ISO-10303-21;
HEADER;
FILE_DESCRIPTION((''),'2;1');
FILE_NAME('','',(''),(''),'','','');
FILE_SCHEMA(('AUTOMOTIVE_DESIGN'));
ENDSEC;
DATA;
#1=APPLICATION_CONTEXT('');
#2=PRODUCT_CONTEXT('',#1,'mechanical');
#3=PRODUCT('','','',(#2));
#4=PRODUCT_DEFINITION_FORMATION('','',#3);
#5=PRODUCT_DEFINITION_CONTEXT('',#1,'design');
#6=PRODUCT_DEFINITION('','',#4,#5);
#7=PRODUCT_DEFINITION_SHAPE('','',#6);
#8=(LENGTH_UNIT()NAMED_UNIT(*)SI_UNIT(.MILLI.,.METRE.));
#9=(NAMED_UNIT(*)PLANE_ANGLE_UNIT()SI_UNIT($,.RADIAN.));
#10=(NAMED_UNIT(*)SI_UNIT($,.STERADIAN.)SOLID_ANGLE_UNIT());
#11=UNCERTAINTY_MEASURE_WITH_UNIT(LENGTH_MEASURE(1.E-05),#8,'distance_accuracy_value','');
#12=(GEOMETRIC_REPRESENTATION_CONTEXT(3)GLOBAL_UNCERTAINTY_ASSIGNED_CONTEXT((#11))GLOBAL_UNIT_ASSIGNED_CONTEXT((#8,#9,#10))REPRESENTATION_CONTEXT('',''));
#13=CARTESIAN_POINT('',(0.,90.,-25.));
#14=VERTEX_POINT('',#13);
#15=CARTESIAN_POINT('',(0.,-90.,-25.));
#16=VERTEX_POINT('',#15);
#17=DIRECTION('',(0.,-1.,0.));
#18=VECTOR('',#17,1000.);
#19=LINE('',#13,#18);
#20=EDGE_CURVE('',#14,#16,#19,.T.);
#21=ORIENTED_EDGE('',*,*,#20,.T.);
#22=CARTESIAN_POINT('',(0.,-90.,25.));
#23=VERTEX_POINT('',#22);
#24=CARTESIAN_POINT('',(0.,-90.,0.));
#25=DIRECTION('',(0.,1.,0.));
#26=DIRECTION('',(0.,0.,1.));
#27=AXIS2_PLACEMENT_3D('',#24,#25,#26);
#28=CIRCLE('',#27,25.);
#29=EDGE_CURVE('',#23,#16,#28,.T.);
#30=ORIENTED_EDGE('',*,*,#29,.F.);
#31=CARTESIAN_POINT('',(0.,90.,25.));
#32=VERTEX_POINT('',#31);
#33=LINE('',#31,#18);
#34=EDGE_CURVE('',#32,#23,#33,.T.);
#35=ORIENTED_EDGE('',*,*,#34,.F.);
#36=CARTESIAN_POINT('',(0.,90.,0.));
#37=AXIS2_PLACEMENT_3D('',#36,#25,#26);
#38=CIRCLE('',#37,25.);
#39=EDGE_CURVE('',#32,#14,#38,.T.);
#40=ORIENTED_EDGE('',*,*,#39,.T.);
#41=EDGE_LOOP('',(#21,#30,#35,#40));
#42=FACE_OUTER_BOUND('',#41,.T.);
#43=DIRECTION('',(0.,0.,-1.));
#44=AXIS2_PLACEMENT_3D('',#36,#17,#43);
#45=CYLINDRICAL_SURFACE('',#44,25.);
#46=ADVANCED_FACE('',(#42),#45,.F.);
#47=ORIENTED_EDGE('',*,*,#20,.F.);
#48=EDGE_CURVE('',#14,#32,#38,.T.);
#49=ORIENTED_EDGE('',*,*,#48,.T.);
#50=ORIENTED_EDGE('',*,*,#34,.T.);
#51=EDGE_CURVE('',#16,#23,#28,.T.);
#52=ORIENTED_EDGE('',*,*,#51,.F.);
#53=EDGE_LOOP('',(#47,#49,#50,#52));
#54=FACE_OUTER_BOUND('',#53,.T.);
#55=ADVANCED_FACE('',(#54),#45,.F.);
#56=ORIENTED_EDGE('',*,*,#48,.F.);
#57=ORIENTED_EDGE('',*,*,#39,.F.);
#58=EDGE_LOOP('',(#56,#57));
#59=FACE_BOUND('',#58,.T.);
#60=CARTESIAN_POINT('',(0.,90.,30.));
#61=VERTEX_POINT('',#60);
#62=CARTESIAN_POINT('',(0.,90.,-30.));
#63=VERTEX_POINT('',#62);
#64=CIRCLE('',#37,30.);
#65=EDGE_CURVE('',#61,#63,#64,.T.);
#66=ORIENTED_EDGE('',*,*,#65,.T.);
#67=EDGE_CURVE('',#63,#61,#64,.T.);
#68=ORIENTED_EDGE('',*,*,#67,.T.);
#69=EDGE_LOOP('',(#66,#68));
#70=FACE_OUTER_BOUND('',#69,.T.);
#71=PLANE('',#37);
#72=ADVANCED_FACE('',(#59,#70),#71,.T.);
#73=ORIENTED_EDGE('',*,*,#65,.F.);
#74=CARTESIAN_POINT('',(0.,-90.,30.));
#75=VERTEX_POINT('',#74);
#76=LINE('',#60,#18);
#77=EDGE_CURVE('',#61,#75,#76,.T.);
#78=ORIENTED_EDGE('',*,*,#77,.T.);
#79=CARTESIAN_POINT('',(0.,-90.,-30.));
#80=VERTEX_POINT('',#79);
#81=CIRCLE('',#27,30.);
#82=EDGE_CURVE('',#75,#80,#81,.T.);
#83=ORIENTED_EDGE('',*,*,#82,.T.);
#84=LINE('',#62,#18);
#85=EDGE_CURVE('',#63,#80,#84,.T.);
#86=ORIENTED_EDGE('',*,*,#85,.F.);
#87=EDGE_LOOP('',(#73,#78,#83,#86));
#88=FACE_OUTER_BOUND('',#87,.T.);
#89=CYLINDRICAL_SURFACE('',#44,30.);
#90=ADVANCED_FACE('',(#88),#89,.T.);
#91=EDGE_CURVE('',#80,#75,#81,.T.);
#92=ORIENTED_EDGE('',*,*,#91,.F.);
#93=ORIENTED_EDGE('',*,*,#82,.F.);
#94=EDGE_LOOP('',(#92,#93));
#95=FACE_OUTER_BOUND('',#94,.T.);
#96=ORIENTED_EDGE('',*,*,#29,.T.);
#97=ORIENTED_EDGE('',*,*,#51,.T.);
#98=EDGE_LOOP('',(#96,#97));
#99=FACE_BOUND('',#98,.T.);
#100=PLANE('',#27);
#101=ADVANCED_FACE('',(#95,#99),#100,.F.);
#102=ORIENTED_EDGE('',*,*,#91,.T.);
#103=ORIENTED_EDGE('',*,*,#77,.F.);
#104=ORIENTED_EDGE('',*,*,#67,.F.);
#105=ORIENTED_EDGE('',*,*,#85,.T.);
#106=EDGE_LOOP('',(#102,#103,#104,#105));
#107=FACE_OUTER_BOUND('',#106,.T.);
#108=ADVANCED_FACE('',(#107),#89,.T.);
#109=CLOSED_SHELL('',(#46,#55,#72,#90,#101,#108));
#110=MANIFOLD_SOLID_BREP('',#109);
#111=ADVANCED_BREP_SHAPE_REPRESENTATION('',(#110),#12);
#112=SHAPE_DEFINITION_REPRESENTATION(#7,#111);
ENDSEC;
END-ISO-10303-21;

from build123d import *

# Parameters (mm, degrees)
SKETCH_1_R           = 30
SKETCH_1_R_2         = 25
BOSS_EXTRUDE_1_DEPTH = 90


with BuildPart() as part:
    # Sketch 1 → Boss-Extrude 1 (new, symmetric)
    with BuildSketch(Plane(origin=(0, 0, 0), x_dir=(1, 0, 0), z_dir=(0, 1, 0))):
        with Locations(Location((0, 0, 0), (0, 0, 90))):
            Circle(SKETCH_1_R)
        with Locations(Location((0, 0, 0), (0, 0, 90))):
            Circle(SKETCH_1_R_2, mode=Mode.SUBTRACT)
    extrude(amount=BOSS_EXTRUDE_1_DEPTH, both=True)


solid = part.part
